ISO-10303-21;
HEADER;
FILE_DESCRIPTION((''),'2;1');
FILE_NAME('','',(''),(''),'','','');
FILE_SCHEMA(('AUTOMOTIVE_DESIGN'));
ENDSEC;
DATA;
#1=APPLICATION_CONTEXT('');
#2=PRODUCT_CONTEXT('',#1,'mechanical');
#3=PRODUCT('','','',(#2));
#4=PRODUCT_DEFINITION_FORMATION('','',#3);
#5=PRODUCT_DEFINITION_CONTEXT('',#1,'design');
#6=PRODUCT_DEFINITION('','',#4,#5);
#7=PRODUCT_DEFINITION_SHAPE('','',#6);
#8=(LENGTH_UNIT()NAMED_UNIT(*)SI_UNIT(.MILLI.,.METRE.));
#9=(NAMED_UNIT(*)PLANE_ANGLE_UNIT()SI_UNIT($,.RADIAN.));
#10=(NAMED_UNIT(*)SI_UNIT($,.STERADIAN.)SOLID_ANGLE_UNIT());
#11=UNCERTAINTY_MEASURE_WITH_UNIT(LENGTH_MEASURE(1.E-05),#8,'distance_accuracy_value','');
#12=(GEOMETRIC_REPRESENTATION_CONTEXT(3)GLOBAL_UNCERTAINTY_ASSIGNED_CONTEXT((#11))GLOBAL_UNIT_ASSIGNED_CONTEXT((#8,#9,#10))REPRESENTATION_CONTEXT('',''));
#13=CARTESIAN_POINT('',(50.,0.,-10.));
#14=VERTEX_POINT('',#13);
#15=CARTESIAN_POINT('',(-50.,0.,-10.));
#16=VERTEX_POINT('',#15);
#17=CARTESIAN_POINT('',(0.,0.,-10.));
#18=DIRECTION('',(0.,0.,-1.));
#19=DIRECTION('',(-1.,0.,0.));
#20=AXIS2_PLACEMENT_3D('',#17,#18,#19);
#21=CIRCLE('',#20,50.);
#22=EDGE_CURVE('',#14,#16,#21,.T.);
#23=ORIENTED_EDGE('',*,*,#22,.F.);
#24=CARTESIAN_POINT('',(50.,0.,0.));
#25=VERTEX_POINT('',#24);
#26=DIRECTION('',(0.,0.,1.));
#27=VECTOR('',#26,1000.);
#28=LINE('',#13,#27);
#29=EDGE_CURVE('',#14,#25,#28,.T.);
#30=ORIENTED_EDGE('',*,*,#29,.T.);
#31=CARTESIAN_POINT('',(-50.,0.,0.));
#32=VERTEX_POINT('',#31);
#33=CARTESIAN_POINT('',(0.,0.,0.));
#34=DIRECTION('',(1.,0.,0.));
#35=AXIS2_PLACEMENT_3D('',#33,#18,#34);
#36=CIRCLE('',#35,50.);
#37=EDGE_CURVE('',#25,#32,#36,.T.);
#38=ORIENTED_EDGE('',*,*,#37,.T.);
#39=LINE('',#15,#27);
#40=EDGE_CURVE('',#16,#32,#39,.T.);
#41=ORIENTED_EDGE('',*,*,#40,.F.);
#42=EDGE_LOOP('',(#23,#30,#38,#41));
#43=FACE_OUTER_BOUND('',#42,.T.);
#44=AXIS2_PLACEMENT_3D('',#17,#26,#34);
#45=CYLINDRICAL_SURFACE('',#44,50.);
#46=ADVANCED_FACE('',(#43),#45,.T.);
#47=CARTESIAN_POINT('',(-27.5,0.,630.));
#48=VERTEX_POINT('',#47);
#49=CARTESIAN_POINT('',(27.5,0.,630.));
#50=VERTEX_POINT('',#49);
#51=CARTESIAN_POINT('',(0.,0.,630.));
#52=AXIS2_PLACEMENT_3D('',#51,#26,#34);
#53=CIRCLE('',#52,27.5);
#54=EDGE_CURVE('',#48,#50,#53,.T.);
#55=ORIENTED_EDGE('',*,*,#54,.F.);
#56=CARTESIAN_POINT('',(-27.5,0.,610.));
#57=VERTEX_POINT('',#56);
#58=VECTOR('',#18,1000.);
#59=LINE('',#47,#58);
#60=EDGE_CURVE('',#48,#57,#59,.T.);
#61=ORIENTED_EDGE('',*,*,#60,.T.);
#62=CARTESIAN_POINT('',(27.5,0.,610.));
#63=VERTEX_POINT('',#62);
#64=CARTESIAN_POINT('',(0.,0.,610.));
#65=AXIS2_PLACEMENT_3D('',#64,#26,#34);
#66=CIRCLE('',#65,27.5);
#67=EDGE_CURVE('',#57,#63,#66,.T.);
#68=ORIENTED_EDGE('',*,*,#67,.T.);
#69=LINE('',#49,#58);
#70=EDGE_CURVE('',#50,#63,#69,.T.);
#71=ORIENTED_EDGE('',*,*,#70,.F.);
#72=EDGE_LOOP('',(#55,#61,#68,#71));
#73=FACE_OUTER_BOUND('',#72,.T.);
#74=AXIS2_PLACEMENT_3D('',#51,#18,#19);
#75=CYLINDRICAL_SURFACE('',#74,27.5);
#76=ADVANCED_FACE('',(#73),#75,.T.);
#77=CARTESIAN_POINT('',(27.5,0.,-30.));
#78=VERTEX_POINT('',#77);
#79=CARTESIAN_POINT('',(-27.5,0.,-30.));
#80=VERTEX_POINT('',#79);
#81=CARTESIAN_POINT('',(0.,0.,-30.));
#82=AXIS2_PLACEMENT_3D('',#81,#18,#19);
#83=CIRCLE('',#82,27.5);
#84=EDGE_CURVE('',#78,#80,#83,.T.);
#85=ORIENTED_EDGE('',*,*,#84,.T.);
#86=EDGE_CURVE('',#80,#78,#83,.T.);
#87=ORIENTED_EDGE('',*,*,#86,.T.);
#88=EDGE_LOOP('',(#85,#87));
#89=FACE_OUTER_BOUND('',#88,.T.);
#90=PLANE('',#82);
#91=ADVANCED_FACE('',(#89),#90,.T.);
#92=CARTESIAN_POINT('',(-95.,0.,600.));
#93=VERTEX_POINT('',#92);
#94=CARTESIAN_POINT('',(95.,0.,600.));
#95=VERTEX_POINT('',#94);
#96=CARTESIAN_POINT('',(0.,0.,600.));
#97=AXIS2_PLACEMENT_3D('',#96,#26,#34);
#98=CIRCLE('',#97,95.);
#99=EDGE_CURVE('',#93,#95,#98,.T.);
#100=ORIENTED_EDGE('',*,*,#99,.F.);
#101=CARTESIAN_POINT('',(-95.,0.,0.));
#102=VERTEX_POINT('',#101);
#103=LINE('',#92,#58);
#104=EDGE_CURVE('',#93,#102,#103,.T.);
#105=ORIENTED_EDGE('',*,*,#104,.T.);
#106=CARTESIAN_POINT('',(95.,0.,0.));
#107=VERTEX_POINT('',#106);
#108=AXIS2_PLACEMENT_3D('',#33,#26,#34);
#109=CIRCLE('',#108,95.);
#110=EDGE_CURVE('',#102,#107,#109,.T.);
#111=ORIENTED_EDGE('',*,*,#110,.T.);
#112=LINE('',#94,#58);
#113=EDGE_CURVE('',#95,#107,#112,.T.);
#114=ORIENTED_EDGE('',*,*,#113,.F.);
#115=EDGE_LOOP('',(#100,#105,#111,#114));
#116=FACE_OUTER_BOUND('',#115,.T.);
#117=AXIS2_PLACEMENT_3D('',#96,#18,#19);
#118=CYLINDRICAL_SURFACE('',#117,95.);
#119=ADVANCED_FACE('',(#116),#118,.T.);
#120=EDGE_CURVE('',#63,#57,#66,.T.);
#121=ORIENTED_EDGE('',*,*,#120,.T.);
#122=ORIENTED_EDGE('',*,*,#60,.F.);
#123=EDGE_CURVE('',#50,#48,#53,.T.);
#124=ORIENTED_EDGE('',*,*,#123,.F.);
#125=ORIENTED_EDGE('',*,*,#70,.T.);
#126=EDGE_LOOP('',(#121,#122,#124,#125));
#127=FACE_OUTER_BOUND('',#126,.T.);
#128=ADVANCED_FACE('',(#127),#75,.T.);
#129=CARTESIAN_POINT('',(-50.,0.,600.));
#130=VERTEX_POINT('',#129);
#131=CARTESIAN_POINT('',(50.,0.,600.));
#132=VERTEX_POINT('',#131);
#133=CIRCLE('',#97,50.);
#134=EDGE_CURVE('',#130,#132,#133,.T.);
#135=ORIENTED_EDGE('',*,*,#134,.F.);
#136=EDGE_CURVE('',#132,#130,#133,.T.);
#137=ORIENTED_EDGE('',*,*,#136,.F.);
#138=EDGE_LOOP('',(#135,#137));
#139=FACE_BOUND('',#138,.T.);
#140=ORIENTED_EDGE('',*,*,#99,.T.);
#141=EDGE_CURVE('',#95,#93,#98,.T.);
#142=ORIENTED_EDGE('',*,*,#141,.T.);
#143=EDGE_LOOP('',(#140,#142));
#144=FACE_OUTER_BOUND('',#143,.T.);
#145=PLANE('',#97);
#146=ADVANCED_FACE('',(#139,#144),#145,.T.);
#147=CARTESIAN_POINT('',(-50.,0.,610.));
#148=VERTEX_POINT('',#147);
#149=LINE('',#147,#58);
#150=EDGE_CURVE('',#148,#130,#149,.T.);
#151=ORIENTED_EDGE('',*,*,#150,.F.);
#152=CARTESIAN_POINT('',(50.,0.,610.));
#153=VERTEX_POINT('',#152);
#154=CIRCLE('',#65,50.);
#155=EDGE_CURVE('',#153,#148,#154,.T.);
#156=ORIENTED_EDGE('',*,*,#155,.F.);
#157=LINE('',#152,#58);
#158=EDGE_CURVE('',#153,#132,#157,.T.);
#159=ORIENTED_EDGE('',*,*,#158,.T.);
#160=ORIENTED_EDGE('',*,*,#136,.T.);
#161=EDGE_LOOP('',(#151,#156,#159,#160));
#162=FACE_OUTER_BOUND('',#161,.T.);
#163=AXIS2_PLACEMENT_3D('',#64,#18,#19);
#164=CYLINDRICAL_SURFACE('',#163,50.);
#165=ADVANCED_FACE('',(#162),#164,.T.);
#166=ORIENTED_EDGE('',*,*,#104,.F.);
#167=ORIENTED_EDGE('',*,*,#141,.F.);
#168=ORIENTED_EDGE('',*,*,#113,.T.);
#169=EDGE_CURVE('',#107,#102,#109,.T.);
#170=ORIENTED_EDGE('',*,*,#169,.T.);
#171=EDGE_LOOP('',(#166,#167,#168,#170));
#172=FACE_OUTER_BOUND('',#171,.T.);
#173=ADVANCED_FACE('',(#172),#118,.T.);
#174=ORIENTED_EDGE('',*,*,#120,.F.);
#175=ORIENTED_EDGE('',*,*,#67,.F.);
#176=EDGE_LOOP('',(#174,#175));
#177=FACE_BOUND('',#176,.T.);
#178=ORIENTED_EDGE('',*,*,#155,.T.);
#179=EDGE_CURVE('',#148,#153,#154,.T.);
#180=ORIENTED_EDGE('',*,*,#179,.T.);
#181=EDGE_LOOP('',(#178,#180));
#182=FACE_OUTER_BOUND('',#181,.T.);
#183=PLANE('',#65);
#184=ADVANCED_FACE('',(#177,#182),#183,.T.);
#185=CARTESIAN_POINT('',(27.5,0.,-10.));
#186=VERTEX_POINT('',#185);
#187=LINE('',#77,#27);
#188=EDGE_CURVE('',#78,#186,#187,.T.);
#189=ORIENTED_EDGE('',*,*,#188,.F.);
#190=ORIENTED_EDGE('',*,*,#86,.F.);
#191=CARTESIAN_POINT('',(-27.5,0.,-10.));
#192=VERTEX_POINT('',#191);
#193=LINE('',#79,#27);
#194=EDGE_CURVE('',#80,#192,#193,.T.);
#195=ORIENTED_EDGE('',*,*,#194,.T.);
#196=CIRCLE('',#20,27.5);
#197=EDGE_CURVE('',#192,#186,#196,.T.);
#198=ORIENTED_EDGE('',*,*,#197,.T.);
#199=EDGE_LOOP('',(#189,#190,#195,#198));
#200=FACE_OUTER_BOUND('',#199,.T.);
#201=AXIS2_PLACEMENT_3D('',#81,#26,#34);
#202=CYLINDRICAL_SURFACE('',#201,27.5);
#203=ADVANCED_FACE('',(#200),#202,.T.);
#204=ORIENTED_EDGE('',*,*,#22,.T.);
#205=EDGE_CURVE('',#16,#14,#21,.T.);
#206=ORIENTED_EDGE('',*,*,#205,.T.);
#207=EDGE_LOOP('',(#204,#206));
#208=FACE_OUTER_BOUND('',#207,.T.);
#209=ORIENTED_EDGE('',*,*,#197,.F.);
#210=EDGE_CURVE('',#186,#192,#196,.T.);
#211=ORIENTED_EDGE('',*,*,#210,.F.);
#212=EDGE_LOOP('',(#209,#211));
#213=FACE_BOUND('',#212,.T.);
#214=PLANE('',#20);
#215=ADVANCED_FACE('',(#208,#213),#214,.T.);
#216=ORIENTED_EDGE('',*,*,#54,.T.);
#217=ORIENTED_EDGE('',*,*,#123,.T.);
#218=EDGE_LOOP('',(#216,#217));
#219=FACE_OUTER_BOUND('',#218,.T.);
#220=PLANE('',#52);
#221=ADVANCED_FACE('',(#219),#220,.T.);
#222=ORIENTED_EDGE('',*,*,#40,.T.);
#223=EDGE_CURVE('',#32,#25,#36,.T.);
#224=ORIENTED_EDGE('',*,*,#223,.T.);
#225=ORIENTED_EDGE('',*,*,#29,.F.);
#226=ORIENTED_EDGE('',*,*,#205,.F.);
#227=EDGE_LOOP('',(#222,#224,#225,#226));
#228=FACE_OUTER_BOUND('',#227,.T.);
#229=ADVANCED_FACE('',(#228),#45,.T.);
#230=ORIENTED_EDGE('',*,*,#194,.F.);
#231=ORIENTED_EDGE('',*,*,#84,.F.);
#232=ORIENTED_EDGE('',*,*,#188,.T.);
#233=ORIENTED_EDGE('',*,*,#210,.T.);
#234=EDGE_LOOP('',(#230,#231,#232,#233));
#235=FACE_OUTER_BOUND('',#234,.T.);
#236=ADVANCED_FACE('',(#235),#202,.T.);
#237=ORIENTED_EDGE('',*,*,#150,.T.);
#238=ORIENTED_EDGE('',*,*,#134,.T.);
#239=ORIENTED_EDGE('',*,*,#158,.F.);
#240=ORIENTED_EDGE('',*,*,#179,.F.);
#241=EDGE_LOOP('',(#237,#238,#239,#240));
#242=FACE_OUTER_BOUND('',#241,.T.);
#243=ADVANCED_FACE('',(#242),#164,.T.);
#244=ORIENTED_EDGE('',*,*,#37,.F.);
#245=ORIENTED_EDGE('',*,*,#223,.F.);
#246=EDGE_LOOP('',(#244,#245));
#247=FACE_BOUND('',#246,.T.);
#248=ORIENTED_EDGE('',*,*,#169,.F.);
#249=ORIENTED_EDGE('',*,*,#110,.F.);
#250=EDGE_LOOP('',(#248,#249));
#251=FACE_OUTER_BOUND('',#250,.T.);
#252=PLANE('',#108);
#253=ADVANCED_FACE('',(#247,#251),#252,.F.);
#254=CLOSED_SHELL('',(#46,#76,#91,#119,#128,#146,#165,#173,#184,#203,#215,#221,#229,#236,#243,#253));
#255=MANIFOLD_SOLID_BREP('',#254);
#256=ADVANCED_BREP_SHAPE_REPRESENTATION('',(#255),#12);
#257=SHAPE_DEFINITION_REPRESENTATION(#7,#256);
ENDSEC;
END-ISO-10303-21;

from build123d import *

# Parameters (mm, degrees)
SKETCH1_R           = 95
BOSS_EXTRUDE1_DEPTH = 600
SKETCH2_R           = 50
BOSS_EXTRUDE2_DEPTH = 10
BOSS_EXTRUDE3_START = 10
SKETCH3_R           = 50
BOSS_EXTRUDE3_DEPTH = 10
SKETCH4_R           = 27.5
BOSS_EXTRUDE4_DEPTH = 20
BOSS_EXTRUDE5_START = 20
SKETCH5_R           = 27.5
BOSS_EXTRUDE5_DEPTH = 20


with BuildPart() as part:
    # Sketch1 → Boss-Extrude1 (new body)
    with BuildSketch(Plane.XY):
        Circle(SKETCH1_R)
    extrude(amount=BOSS_EXTRUDE1_DEPTH)

    # Sketch2 → Boss-Extrude2 (add)
    with BuildSketch(Plane.XY.offset(600)):
        Circle(SKETCH2_R)
    extrude(amount=BOSS_EXTRUDE2_DEPTH)

    # Sketch3 → Boss-Extrude3 (add)
    with BuildSketch(Plane(origin=(0, 0, 0), x_dir=(-1, 0, 0), z_dir=(0, 0, -1)).offset(BOSS_EXTRUDE3_START)):
        with Locations(Location((0, 0, 0), (0, 0, 180))):
            Circle(SKETCH3_R)
    extrude(amount=-BOSS_EXTRUDE3_DEPTH)

    # Sketch4 → Boss-Extrude4 (add)
    with BuildSketch(Plane(origin=(0, 0, -10), x_dir=(-1, 0, 0), z_dir=(0, 0, -1))):
        Circle(SKETCH4_R)
    extrude(amount=BOSS_EXTRUDE4_DEPTH)

    # Sketch5 → Boss-Extrude5 (add)
    with BuildSketch(Plane.XY.offset(610).offset(BOSS_EXTRUDE5_START)):
        with Locations(Location((0, 0, 0), (0, 0, 180))):
            Circle(SKETCH5_R)
    extrude(amount=-BOSS_EXTRUDE5_DEPTH)


solid = part.part
